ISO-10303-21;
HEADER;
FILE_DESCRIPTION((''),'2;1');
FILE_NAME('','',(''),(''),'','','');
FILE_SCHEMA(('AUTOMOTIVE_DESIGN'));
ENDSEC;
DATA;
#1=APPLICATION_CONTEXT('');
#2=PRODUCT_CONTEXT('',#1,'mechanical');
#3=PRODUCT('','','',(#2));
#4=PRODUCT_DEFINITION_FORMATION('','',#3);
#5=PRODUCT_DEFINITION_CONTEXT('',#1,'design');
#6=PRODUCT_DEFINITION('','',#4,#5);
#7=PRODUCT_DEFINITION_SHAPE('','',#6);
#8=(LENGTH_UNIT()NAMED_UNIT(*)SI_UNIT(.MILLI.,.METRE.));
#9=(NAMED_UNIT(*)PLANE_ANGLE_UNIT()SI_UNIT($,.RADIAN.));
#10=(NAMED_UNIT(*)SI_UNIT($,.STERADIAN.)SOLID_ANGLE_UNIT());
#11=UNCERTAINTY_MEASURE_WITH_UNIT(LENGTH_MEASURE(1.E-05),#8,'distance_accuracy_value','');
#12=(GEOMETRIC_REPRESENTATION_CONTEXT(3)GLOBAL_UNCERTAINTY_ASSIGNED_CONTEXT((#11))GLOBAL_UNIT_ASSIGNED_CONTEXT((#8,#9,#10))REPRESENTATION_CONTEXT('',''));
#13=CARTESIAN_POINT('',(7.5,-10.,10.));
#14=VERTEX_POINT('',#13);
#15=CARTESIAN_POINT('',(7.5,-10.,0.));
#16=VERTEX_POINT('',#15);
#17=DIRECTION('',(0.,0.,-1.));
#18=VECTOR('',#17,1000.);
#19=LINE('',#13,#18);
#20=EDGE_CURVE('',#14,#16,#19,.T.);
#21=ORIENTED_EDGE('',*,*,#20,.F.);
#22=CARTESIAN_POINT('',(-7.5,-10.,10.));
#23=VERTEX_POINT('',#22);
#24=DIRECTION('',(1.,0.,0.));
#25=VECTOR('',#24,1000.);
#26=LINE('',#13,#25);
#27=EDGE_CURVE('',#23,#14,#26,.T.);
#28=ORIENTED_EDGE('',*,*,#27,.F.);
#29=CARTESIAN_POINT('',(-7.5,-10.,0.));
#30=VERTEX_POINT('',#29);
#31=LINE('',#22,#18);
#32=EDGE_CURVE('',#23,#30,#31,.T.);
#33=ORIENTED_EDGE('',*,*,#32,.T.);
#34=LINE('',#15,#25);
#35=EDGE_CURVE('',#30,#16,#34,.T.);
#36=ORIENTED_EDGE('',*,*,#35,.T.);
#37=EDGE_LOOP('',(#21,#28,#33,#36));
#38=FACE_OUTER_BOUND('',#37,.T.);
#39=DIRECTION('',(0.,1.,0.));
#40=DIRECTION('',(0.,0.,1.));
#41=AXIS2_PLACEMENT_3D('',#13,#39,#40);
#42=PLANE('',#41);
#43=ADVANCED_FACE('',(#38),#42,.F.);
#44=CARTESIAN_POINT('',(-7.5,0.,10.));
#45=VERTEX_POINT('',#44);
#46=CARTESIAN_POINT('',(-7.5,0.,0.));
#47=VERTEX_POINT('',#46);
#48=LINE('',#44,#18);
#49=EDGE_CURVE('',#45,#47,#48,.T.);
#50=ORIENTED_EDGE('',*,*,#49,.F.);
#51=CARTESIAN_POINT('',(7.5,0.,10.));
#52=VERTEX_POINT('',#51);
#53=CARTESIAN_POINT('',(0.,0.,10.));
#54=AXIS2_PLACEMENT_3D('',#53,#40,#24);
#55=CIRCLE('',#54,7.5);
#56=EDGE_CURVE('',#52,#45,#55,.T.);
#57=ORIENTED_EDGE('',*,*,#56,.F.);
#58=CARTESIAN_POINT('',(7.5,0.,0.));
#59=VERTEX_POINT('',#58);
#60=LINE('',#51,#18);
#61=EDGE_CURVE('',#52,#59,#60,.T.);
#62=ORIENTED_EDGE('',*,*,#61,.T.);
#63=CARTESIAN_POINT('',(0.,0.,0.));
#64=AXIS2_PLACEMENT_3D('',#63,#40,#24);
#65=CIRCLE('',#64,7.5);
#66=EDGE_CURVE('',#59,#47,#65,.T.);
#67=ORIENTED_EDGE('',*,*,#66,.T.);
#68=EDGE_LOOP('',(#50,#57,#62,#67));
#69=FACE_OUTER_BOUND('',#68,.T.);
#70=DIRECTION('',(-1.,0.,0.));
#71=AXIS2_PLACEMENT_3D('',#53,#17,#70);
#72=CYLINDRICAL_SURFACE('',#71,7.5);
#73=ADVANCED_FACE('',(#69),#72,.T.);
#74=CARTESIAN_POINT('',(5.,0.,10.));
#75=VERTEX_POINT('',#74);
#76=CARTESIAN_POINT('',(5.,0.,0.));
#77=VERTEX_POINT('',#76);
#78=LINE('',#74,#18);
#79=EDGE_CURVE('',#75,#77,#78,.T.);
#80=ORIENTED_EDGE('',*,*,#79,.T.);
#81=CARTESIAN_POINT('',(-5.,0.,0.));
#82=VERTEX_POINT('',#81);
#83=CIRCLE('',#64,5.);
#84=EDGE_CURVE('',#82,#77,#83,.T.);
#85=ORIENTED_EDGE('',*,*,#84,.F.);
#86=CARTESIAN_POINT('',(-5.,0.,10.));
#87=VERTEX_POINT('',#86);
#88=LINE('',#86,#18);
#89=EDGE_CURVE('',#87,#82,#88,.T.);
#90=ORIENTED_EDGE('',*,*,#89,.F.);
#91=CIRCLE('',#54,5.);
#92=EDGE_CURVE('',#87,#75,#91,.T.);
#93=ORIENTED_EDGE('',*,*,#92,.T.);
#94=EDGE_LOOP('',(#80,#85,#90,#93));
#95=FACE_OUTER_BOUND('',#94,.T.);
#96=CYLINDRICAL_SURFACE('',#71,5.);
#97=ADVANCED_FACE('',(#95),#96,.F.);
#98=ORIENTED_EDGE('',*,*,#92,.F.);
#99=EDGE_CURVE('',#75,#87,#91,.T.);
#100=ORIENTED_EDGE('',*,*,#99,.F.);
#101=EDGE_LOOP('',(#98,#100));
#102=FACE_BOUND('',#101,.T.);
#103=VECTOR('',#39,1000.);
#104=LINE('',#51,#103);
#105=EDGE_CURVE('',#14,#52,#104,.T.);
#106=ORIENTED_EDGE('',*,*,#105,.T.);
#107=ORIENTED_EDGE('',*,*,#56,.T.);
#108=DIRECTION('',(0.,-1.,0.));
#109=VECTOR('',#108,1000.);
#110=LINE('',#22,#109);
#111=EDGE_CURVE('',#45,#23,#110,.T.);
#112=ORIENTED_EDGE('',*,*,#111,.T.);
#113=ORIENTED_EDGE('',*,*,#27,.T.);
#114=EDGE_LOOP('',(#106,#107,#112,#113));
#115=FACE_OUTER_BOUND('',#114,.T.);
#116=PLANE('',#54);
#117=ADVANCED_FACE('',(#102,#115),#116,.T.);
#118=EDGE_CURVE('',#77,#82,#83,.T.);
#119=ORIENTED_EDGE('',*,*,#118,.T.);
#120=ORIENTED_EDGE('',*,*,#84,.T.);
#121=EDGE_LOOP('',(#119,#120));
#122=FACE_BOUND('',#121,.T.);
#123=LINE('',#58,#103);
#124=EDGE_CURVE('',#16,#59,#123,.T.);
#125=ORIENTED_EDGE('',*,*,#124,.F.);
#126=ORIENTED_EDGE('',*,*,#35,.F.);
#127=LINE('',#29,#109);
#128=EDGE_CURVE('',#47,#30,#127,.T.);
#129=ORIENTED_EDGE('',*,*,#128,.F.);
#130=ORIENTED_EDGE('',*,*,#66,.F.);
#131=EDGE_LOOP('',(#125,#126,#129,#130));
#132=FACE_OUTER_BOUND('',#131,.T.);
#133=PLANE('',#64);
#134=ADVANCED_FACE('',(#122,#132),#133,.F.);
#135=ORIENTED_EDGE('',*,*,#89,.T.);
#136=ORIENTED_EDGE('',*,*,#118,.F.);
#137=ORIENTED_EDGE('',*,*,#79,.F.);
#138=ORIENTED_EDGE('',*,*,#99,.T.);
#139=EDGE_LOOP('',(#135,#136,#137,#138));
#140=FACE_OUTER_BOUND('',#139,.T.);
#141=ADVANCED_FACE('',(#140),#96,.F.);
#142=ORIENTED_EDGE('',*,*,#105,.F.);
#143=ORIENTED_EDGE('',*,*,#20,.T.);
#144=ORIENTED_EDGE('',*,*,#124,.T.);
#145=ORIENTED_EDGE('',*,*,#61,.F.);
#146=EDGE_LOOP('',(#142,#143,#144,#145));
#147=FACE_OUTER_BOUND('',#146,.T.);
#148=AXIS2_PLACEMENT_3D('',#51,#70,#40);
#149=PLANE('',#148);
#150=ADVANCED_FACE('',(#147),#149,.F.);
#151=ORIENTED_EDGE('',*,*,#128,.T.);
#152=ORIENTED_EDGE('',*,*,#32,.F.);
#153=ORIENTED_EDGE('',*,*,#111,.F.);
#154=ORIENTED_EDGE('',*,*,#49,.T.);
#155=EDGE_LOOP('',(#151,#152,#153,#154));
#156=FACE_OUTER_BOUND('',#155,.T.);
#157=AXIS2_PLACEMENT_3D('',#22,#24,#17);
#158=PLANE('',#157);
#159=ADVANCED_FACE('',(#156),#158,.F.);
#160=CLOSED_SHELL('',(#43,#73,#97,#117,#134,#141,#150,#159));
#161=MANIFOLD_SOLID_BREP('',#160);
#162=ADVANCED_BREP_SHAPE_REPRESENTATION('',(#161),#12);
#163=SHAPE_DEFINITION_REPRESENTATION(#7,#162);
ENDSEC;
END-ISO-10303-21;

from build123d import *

# Parameters (mm, degrees)
SKETCH_1_R      = 5
EXTRUDE_1_DEPTH = 10


with BuildPart() as part:
    # 草图1 → 凸台-拉伸1 (new body)
    with BuildSketch(Plane.XY):
        with BuildLine():
            Line((7.5, 0), (7.5, -10))
            Line((7.5, -10), (-7.5, -10))
            Line((-7.5, -10), (-7.5, 0))
            ThreePointArc((-7.5, 0), (0, 7.5), (7.5, 0))
        make_face()
        Circle(SKETCH_1_R, mode=Mode.SUBTRACT)
    extrude(amount=EXTRUDE_1_DEPTH)


solid = part.part
